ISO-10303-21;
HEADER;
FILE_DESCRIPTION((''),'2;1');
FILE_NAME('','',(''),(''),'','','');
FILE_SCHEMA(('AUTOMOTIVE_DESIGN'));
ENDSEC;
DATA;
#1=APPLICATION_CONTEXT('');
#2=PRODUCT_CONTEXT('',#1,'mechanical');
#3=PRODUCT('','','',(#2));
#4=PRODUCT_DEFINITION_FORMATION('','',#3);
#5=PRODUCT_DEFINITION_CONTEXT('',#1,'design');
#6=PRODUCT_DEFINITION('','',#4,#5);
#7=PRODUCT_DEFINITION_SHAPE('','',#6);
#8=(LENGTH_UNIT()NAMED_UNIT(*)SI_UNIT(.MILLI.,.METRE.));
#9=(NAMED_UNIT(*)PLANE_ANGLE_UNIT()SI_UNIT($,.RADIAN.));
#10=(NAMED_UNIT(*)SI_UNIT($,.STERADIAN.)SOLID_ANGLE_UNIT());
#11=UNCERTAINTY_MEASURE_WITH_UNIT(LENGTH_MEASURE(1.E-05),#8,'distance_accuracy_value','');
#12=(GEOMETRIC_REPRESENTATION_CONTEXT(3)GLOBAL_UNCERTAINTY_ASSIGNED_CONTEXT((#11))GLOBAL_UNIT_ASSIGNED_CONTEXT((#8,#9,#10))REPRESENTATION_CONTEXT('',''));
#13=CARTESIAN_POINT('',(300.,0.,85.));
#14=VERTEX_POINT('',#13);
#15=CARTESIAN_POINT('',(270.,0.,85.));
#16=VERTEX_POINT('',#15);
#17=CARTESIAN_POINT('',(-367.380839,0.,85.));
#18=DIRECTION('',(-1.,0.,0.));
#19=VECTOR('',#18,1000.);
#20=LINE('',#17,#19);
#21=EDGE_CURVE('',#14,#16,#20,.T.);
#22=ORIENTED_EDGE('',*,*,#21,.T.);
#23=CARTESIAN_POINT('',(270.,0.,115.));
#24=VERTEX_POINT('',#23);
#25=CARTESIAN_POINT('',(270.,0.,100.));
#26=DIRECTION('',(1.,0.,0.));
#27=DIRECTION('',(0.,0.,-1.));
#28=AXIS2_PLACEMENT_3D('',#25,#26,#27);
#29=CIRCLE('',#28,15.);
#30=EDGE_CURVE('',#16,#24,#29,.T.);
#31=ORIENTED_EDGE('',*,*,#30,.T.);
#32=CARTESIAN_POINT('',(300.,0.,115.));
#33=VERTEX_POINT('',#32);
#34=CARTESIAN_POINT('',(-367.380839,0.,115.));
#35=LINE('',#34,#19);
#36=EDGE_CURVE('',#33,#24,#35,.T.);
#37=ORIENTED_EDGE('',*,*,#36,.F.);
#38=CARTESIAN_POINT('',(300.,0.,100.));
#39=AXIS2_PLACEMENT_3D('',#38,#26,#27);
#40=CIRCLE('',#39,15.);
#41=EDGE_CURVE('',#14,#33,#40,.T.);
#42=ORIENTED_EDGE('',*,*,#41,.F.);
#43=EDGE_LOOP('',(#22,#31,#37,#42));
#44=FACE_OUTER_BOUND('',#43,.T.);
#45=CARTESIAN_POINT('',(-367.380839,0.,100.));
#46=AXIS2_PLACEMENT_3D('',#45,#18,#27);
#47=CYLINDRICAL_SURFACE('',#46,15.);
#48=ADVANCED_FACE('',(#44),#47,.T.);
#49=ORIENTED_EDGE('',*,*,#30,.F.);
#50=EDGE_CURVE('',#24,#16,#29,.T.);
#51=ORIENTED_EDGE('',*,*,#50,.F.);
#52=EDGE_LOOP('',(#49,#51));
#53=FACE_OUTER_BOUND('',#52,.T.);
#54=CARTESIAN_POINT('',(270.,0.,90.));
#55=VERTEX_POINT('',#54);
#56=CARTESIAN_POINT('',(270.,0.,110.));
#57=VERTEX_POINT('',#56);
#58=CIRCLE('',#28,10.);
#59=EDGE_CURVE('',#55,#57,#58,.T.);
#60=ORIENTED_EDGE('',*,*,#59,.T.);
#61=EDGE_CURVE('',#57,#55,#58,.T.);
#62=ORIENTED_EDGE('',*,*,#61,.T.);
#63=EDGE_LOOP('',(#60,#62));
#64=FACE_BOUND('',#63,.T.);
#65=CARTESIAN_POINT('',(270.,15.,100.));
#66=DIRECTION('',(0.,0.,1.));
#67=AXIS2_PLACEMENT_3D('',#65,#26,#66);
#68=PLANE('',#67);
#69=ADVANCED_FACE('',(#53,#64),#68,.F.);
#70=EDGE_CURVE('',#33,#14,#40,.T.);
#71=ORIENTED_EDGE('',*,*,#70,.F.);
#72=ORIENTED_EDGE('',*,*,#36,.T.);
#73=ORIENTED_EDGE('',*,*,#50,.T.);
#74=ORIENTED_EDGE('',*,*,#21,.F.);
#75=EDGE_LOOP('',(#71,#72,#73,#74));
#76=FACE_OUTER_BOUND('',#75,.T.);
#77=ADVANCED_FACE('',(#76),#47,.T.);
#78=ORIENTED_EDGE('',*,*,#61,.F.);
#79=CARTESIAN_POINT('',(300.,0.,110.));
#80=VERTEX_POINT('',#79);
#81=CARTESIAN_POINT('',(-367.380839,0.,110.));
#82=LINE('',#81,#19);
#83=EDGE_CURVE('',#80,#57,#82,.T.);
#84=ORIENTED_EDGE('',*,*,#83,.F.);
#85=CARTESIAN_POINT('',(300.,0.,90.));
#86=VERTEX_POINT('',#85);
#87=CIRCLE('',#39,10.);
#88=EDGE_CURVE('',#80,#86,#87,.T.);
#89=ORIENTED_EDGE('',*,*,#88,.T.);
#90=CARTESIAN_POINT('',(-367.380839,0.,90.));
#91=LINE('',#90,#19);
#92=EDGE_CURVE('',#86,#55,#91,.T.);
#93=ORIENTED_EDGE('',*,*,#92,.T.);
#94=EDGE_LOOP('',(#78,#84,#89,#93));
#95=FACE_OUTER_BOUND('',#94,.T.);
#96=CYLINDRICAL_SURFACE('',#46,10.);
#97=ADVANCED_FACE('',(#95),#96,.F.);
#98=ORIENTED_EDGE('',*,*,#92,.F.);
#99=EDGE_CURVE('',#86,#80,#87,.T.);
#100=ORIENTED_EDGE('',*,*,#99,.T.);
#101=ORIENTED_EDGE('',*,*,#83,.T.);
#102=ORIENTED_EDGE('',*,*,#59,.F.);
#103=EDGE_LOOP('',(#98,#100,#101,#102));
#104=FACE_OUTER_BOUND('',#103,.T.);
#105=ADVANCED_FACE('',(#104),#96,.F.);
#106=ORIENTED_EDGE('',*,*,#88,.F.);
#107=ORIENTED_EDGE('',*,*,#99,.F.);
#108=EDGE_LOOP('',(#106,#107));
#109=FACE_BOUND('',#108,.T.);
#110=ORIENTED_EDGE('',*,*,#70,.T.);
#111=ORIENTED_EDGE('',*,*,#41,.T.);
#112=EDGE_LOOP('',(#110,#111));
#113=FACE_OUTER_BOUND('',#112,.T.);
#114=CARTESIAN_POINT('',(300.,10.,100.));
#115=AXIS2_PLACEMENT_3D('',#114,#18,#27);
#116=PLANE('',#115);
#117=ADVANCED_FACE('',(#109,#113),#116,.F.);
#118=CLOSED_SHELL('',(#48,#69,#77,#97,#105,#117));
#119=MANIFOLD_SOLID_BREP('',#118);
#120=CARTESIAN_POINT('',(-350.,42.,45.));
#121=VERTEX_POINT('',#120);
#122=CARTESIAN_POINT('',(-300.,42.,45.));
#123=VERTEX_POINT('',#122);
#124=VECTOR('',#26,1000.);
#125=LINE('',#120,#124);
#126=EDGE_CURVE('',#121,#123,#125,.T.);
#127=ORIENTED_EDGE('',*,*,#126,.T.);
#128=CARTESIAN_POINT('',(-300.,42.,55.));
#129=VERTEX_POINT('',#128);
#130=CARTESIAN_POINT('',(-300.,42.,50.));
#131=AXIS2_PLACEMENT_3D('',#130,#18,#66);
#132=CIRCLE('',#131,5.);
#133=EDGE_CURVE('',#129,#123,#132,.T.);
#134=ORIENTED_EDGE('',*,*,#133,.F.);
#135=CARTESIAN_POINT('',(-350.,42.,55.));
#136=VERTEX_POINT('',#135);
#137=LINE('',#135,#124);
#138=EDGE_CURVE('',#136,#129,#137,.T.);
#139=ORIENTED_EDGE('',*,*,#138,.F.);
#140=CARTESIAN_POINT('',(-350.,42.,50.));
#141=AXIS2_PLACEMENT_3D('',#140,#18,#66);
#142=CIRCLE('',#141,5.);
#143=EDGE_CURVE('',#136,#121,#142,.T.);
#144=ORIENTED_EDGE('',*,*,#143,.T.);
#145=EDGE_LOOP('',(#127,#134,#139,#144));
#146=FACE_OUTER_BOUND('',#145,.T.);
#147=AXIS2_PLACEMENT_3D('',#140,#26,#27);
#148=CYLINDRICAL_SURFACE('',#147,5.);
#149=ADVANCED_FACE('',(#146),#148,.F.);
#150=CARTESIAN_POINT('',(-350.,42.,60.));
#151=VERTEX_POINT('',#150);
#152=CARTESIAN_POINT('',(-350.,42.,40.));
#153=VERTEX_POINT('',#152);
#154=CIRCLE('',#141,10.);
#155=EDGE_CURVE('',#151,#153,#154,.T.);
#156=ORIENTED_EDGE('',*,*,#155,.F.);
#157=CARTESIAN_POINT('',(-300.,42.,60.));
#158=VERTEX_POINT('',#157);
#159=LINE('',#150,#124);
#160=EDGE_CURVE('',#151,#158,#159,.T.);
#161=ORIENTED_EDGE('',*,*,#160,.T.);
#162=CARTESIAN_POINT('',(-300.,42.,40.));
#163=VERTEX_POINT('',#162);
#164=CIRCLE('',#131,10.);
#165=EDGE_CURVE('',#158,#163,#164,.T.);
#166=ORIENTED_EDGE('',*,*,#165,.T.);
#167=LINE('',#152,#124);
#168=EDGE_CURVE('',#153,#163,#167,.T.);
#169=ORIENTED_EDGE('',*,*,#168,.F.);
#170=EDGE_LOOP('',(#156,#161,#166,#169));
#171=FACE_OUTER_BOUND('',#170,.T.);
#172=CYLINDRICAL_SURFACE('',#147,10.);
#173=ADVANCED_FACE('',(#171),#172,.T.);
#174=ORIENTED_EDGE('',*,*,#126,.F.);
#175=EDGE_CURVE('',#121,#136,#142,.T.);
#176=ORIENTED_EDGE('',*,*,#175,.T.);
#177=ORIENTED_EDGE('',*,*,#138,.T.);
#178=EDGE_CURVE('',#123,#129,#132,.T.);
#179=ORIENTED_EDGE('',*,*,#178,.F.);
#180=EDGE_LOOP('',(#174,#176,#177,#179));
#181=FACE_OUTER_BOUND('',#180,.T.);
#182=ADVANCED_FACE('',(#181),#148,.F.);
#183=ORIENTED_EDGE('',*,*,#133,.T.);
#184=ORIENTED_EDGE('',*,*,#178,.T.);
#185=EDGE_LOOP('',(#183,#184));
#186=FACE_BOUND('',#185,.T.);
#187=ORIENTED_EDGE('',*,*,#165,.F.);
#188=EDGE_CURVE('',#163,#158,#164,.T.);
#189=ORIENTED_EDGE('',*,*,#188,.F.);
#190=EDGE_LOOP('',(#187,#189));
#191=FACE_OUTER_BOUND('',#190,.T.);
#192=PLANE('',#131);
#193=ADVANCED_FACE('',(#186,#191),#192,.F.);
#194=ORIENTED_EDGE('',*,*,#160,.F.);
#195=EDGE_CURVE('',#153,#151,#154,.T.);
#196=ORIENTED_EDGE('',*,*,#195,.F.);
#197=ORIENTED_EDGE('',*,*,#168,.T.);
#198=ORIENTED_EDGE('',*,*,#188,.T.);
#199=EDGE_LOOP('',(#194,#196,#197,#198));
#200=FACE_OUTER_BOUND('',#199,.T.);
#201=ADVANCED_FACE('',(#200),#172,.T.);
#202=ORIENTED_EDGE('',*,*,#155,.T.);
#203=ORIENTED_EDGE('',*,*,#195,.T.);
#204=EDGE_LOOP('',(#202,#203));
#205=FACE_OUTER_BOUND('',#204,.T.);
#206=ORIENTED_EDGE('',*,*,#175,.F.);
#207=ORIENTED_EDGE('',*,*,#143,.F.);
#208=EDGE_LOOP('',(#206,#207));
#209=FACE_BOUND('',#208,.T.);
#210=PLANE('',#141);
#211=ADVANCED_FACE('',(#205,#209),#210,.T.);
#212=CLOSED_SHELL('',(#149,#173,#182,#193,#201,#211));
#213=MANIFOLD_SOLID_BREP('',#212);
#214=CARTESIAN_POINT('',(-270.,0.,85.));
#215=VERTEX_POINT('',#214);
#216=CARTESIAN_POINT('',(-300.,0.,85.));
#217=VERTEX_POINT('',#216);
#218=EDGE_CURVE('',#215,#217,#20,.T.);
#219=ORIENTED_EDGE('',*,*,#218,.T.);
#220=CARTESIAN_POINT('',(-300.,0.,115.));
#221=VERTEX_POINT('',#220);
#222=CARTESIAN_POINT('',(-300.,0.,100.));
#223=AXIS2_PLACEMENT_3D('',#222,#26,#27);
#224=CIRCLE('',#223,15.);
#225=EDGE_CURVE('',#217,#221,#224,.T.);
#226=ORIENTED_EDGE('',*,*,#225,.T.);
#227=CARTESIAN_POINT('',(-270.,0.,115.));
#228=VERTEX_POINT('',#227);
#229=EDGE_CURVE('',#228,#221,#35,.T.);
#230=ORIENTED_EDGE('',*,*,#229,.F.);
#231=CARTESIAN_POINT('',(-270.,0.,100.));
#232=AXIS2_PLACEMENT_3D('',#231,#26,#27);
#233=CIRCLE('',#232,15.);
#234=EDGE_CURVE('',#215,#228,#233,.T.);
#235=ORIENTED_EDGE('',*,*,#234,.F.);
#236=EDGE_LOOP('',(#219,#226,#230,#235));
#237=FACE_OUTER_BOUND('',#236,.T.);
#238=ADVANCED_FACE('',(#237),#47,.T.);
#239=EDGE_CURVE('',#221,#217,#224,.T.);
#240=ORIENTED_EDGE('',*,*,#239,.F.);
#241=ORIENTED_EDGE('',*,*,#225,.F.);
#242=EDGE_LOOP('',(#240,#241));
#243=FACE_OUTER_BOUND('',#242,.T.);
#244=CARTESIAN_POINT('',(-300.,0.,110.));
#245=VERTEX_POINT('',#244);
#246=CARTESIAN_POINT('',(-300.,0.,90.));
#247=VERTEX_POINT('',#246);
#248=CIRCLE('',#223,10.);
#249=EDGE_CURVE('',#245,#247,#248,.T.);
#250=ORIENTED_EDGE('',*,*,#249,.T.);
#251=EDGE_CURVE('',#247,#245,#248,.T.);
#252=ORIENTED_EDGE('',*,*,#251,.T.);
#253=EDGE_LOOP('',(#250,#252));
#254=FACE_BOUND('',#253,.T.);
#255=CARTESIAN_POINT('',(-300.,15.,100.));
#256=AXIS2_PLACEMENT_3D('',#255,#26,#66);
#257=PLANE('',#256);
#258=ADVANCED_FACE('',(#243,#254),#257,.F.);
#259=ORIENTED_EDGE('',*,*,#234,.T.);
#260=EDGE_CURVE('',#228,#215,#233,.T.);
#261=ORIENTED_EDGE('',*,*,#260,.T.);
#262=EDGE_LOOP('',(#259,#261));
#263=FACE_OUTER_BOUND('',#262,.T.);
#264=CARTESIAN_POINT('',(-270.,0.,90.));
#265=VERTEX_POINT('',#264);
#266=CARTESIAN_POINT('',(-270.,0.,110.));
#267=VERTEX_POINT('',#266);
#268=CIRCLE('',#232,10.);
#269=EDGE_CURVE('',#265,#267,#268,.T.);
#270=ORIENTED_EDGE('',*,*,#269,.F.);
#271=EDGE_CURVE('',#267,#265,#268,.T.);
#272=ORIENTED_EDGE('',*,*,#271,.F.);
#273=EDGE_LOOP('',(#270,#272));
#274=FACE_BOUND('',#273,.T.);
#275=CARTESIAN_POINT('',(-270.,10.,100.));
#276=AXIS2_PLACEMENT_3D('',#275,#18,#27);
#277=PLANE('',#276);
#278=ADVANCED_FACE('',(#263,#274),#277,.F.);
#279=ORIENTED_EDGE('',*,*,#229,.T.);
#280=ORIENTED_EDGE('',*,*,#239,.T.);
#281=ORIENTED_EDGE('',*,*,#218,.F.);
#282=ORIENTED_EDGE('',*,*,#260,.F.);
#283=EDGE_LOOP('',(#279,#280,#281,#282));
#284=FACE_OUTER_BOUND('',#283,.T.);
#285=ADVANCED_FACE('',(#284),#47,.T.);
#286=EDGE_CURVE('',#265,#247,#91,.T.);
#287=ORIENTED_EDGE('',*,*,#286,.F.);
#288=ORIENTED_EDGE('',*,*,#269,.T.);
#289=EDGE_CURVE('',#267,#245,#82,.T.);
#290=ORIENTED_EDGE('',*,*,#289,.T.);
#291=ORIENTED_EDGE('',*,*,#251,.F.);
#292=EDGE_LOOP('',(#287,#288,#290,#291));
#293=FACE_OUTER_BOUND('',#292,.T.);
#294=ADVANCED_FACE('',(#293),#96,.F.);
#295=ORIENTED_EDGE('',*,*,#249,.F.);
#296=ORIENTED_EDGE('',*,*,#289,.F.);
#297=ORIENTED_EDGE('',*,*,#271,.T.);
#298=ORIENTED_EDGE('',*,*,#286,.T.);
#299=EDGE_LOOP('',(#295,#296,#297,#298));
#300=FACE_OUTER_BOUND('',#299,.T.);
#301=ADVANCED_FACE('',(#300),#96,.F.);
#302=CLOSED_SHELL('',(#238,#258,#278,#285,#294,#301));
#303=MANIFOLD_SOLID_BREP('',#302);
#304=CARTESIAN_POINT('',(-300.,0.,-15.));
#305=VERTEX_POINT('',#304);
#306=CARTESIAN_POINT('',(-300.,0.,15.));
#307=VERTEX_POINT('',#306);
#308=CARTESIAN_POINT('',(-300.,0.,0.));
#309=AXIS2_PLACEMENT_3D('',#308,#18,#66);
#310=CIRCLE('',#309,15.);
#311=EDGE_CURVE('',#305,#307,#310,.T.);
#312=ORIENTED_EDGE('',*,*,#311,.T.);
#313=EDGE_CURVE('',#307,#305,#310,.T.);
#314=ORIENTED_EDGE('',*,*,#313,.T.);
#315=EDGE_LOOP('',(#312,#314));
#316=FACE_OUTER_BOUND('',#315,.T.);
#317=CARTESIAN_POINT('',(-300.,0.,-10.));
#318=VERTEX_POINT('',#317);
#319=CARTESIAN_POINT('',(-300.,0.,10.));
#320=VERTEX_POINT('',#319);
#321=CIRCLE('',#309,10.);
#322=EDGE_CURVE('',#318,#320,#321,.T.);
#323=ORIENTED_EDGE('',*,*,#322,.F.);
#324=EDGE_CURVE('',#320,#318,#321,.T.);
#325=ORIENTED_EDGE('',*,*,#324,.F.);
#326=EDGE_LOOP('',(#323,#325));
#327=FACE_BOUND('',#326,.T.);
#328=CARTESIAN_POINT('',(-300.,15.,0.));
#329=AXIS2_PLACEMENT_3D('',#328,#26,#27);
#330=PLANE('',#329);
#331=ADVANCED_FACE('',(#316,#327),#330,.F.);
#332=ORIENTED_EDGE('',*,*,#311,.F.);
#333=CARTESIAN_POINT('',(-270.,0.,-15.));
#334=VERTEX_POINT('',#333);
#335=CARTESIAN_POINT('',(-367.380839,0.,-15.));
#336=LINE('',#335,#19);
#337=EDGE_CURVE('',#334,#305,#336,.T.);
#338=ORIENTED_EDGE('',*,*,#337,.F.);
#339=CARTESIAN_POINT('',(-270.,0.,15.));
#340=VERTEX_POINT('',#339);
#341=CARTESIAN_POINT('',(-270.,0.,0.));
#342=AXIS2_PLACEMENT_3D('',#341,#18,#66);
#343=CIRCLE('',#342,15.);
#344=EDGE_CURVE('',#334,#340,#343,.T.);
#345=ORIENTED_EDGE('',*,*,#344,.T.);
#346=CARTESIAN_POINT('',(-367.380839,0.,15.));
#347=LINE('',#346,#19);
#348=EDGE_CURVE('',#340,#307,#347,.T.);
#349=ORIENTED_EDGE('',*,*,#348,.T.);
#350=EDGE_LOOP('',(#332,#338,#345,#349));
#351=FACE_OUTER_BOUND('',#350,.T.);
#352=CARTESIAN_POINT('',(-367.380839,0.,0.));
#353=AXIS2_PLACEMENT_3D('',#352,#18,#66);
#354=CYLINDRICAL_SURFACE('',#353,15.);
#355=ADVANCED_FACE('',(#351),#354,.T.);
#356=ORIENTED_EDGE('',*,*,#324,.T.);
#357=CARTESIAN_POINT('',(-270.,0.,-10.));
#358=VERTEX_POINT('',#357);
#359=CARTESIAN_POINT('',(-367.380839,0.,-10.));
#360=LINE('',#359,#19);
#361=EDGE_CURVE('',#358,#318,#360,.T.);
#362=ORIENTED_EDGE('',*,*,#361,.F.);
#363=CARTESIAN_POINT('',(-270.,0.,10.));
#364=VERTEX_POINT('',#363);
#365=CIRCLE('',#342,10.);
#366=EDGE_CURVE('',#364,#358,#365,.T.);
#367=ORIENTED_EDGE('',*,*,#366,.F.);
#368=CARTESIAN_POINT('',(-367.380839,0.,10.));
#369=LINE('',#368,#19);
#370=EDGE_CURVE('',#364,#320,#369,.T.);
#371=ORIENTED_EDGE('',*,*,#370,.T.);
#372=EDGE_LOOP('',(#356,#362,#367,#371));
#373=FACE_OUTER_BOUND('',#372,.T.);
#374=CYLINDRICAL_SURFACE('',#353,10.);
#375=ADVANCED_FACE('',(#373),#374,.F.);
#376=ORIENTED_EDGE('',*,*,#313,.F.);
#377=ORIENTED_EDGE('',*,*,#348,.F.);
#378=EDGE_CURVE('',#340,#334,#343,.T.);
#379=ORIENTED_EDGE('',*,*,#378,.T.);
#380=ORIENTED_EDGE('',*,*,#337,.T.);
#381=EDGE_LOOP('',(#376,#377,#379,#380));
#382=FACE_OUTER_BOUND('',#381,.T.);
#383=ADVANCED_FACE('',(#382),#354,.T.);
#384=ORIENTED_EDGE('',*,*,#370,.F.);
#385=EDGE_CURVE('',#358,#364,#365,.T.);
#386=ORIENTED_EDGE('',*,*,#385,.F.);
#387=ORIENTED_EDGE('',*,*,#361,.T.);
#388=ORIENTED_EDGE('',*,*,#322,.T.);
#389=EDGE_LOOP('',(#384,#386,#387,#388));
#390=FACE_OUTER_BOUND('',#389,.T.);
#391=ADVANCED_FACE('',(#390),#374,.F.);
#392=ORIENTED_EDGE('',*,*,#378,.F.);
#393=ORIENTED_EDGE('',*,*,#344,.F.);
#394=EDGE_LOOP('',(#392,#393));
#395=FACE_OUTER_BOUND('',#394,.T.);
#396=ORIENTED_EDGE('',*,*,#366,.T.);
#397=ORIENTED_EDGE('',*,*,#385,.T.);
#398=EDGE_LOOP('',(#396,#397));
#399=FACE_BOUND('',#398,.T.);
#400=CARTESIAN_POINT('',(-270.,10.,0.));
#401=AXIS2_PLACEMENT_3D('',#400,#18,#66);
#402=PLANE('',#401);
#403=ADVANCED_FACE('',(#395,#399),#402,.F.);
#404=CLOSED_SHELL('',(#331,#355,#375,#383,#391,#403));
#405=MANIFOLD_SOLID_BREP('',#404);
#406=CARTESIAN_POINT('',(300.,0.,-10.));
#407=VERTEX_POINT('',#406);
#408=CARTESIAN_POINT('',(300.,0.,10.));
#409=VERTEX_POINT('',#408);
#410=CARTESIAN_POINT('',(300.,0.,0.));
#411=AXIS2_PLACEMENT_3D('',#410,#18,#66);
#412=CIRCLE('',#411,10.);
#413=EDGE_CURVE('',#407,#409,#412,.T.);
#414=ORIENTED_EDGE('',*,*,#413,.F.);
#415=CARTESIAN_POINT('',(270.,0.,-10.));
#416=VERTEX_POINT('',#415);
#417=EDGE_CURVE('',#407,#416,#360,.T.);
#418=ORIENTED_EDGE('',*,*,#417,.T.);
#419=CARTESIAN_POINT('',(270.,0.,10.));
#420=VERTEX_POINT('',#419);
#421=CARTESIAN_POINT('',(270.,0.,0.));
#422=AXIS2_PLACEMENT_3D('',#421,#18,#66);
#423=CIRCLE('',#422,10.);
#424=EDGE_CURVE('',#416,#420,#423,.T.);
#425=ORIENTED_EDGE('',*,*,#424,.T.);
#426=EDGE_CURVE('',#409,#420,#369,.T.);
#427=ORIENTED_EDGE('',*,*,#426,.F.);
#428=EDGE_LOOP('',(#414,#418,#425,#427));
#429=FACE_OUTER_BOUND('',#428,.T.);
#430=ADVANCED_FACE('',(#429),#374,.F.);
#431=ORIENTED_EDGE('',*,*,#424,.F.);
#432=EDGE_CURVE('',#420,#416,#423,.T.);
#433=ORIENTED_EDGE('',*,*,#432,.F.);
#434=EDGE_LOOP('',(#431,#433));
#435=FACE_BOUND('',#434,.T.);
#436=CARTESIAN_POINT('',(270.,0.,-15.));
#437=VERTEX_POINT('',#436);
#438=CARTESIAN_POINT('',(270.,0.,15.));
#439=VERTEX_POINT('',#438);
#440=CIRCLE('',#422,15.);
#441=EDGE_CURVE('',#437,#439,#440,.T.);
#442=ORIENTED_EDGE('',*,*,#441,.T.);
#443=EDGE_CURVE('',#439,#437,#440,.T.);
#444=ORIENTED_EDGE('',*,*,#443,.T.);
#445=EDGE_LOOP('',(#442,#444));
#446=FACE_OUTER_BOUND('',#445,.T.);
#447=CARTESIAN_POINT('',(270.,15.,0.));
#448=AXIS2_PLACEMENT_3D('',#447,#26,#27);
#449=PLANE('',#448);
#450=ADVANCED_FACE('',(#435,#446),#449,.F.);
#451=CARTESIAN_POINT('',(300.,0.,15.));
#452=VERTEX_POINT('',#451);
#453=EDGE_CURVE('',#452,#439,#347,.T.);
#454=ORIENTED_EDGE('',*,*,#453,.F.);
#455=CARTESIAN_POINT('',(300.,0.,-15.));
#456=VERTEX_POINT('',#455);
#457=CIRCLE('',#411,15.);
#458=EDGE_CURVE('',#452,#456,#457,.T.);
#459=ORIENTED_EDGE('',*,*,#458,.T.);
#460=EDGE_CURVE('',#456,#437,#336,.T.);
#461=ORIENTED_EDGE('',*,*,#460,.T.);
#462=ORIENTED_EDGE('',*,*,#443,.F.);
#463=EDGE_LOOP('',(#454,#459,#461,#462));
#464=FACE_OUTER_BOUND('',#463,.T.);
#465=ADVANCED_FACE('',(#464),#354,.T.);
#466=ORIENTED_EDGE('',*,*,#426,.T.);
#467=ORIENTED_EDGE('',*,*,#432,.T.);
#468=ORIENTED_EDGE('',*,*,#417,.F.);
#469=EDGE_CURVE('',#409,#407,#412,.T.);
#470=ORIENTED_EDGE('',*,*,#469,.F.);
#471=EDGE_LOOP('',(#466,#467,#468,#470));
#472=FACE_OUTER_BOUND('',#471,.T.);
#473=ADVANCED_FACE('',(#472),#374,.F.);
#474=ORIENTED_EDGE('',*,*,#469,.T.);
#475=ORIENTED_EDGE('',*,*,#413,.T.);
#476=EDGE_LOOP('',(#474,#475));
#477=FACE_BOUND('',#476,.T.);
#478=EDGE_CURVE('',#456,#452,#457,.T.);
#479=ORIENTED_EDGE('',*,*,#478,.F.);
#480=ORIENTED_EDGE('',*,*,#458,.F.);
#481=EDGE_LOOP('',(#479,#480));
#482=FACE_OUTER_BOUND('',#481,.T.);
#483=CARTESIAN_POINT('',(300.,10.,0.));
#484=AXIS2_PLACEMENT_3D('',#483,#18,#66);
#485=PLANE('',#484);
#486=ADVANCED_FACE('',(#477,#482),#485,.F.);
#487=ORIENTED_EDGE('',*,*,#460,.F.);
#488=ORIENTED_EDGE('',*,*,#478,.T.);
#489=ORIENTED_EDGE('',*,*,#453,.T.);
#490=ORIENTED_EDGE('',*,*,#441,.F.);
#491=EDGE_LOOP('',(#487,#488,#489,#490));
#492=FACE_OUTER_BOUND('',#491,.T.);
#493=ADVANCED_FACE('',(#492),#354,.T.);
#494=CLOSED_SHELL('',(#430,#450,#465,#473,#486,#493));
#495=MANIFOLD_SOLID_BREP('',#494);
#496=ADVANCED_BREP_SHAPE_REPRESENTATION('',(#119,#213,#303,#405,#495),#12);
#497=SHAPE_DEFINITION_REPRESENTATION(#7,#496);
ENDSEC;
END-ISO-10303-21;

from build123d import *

# Parameters (mm, degrees)
SKETCH1_W           = 30
SKETCH1_H           = 5
SKETCH3_R           = 10
SKETCH3_R_2         = 5
BOSS_EXTRUDE1_DEPTH = 50


with BuildPart() as part:
    # Sketch1 → Revolve1 (revolve)
    with BuildSketch(Plane.XY, mode=Mode.PRIVATE) as revolve1_sk:
        with Locations((-285, 12.5)):
            Rectangle(SKETCH1_W, SKETCH1_H)
        with Locations((285, 12.5)):
            Rectangle(SKETCH1_W, SKETCH1_H)
    revolve(revolve1_sk.sketch.rotate(Axis((-367.380839301, 0, 0), (1, 0, 0)), 90), axis=Axis((-367.380839301, 0, 0), (1, 0, 0)))


with BuildPart() as body_2:
    # Mirror5: mirrored copy
    add(part.part.mirror(Plane.XY.offset(50)))


with BuildPart() as body_3:
    # Sketch3 → Boss-Extrude1 (new body)
    with BuildSketch(Plane.ZY.offset(300)):
        with Locations((50, 42)):
            Circle(SKETCH3_R)
        with Locations((50, 42)):
            Circle(SKETCH3_R_2, mode=Mode.SUBTRACT)
    extrude(amount=BOSS_EXTRUDE1_DEPTH)


solid = Compound([part.part, body_2.part, body_3.part])
